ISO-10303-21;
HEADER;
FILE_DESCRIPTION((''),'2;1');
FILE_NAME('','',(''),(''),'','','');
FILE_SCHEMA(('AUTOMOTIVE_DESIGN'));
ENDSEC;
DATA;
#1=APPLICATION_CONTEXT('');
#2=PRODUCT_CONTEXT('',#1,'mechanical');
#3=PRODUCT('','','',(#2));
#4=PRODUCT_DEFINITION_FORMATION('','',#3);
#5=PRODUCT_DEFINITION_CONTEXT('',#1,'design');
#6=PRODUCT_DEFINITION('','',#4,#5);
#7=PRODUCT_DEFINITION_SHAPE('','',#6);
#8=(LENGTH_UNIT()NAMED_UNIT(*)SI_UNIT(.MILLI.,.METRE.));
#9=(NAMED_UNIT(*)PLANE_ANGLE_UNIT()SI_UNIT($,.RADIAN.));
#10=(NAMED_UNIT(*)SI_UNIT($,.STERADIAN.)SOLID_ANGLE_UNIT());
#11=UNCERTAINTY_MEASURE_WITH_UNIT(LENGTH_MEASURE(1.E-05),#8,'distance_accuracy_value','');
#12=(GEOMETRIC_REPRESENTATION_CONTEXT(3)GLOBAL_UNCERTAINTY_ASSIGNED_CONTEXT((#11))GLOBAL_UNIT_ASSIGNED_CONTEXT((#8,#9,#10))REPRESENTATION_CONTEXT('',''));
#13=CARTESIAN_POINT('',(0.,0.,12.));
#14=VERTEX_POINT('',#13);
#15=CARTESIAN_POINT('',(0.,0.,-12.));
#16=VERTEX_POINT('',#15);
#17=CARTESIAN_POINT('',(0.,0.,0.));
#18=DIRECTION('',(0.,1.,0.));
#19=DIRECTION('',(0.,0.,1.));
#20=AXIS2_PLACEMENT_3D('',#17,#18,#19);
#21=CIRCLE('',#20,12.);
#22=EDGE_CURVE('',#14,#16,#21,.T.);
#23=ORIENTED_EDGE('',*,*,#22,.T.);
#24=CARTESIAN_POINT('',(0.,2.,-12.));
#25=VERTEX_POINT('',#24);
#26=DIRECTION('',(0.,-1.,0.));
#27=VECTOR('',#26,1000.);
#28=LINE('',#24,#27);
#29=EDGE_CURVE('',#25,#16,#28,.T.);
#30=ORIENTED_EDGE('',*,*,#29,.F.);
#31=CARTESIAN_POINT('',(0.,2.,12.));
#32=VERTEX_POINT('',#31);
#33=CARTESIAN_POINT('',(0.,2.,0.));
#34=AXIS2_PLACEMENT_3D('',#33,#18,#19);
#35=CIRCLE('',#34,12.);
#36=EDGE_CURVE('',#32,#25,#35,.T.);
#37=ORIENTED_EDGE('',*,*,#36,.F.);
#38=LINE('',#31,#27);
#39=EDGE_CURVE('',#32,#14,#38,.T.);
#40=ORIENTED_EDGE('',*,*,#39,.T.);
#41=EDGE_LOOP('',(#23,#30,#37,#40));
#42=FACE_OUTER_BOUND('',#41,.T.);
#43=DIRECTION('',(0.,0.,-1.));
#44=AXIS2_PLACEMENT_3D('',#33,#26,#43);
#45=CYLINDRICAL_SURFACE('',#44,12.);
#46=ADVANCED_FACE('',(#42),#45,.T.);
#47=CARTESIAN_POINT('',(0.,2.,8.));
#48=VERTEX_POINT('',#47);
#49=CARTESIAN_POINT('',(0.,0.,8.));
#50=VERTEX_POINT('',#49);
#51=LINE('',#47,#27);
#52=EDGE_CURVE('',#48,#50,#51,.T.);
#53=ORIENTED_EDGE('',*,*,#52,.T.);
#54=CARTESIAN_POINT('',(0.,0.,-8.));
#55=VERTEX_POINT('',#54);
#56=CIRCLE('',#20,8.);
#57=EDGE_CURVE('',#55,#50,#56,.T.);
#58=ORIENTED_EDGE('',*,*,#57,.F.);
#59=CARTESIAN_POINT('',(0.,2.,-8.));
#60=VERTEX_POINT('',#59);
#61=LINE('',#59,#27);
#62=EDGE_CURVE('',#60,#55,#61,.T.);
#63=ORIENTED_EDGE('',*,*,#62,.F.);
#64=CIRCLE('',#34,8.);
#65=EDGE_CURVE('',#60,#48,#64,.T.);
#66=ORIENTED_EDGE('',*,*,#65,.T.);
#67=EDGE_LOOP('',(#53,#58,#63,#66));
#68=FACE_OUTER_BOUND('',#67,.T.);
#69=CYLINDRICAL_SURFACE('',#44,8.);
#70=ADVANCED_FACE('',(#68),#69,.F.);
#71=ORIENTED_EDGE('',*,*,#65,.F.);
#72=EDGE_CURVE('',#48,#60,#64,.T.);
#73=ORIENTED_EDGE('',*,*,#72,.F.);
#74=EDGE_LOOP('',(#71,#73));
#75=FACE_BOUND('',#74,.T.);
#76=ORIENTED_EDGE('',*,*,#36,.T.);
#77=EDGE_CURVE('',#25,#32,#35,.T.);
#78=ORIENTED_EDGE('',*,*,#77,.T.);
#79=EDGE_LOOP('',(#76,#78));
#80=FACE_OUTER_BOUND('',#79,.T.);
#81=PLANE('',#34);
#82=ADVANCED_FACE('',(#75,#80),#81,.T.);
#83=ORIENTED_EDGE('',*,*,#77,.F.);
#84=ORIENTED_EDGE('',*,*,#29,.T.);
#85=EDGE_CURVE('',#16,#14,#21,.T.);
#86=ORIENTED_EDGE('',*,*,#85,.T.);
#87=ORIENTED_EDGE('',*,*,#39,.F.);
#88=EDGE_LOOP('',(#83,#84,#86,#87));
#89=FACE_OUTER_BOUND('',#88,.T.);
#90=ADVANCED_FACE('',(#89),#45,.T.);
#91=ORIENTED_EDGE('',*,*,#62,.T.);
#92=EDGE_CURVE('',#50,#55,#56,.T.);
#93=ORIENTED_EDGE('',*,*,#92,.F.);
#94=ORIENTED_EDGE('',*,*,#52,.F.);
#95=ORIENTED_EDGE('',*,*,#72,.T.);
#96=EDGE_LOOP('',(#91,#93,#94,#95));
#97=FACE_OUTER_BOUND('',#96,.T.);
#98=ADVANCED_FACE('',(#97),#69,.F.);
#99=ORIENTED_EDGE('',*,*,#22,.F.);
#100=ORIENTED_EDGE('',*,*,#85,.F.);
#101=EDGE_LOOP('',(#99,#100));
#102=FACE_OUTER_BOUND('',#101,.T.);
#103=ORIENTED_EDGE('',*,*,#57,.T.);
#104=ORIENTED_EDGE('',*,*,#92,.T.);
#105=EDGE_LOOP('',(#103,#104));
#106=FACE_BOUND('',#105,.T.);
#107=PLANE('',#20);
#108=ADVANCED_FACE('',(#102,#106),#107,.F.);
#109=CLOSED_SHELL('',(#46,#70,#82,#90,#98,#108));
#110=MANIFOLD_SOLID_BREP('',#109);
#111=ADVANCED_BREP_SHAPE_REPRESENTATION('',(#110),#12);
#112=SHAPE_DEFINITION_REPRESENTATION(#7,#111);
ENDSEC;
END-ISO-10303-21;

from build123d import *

# Parameters (mm, degrees)
SKETCH1_R           = 12
SKETCH1_R_2         = 8
BOSS_EXTRUDE3_DEPTH = 2


with BuildPart() as part:
    # Sketch1 → Boss-Extrude3 (new body)
    with BuildSketch(Plane(origin=(0, 0, 0), x_dir=(1, 0, 0), z_dir=(0, 1, 0))):
        with Locations(Location((0, 0, 0), (0, 0, 270))):
            Circle(SKETCH1_R)
        with Locations(Location((0, 0, 0), (0, 0, 270))):
            Circle(SKETCH1_R_2, mode=Mode.SUBTRACT)
    extrude(amount=BOSS_EXTRUDE3_DEPTH)


solid = part.part
